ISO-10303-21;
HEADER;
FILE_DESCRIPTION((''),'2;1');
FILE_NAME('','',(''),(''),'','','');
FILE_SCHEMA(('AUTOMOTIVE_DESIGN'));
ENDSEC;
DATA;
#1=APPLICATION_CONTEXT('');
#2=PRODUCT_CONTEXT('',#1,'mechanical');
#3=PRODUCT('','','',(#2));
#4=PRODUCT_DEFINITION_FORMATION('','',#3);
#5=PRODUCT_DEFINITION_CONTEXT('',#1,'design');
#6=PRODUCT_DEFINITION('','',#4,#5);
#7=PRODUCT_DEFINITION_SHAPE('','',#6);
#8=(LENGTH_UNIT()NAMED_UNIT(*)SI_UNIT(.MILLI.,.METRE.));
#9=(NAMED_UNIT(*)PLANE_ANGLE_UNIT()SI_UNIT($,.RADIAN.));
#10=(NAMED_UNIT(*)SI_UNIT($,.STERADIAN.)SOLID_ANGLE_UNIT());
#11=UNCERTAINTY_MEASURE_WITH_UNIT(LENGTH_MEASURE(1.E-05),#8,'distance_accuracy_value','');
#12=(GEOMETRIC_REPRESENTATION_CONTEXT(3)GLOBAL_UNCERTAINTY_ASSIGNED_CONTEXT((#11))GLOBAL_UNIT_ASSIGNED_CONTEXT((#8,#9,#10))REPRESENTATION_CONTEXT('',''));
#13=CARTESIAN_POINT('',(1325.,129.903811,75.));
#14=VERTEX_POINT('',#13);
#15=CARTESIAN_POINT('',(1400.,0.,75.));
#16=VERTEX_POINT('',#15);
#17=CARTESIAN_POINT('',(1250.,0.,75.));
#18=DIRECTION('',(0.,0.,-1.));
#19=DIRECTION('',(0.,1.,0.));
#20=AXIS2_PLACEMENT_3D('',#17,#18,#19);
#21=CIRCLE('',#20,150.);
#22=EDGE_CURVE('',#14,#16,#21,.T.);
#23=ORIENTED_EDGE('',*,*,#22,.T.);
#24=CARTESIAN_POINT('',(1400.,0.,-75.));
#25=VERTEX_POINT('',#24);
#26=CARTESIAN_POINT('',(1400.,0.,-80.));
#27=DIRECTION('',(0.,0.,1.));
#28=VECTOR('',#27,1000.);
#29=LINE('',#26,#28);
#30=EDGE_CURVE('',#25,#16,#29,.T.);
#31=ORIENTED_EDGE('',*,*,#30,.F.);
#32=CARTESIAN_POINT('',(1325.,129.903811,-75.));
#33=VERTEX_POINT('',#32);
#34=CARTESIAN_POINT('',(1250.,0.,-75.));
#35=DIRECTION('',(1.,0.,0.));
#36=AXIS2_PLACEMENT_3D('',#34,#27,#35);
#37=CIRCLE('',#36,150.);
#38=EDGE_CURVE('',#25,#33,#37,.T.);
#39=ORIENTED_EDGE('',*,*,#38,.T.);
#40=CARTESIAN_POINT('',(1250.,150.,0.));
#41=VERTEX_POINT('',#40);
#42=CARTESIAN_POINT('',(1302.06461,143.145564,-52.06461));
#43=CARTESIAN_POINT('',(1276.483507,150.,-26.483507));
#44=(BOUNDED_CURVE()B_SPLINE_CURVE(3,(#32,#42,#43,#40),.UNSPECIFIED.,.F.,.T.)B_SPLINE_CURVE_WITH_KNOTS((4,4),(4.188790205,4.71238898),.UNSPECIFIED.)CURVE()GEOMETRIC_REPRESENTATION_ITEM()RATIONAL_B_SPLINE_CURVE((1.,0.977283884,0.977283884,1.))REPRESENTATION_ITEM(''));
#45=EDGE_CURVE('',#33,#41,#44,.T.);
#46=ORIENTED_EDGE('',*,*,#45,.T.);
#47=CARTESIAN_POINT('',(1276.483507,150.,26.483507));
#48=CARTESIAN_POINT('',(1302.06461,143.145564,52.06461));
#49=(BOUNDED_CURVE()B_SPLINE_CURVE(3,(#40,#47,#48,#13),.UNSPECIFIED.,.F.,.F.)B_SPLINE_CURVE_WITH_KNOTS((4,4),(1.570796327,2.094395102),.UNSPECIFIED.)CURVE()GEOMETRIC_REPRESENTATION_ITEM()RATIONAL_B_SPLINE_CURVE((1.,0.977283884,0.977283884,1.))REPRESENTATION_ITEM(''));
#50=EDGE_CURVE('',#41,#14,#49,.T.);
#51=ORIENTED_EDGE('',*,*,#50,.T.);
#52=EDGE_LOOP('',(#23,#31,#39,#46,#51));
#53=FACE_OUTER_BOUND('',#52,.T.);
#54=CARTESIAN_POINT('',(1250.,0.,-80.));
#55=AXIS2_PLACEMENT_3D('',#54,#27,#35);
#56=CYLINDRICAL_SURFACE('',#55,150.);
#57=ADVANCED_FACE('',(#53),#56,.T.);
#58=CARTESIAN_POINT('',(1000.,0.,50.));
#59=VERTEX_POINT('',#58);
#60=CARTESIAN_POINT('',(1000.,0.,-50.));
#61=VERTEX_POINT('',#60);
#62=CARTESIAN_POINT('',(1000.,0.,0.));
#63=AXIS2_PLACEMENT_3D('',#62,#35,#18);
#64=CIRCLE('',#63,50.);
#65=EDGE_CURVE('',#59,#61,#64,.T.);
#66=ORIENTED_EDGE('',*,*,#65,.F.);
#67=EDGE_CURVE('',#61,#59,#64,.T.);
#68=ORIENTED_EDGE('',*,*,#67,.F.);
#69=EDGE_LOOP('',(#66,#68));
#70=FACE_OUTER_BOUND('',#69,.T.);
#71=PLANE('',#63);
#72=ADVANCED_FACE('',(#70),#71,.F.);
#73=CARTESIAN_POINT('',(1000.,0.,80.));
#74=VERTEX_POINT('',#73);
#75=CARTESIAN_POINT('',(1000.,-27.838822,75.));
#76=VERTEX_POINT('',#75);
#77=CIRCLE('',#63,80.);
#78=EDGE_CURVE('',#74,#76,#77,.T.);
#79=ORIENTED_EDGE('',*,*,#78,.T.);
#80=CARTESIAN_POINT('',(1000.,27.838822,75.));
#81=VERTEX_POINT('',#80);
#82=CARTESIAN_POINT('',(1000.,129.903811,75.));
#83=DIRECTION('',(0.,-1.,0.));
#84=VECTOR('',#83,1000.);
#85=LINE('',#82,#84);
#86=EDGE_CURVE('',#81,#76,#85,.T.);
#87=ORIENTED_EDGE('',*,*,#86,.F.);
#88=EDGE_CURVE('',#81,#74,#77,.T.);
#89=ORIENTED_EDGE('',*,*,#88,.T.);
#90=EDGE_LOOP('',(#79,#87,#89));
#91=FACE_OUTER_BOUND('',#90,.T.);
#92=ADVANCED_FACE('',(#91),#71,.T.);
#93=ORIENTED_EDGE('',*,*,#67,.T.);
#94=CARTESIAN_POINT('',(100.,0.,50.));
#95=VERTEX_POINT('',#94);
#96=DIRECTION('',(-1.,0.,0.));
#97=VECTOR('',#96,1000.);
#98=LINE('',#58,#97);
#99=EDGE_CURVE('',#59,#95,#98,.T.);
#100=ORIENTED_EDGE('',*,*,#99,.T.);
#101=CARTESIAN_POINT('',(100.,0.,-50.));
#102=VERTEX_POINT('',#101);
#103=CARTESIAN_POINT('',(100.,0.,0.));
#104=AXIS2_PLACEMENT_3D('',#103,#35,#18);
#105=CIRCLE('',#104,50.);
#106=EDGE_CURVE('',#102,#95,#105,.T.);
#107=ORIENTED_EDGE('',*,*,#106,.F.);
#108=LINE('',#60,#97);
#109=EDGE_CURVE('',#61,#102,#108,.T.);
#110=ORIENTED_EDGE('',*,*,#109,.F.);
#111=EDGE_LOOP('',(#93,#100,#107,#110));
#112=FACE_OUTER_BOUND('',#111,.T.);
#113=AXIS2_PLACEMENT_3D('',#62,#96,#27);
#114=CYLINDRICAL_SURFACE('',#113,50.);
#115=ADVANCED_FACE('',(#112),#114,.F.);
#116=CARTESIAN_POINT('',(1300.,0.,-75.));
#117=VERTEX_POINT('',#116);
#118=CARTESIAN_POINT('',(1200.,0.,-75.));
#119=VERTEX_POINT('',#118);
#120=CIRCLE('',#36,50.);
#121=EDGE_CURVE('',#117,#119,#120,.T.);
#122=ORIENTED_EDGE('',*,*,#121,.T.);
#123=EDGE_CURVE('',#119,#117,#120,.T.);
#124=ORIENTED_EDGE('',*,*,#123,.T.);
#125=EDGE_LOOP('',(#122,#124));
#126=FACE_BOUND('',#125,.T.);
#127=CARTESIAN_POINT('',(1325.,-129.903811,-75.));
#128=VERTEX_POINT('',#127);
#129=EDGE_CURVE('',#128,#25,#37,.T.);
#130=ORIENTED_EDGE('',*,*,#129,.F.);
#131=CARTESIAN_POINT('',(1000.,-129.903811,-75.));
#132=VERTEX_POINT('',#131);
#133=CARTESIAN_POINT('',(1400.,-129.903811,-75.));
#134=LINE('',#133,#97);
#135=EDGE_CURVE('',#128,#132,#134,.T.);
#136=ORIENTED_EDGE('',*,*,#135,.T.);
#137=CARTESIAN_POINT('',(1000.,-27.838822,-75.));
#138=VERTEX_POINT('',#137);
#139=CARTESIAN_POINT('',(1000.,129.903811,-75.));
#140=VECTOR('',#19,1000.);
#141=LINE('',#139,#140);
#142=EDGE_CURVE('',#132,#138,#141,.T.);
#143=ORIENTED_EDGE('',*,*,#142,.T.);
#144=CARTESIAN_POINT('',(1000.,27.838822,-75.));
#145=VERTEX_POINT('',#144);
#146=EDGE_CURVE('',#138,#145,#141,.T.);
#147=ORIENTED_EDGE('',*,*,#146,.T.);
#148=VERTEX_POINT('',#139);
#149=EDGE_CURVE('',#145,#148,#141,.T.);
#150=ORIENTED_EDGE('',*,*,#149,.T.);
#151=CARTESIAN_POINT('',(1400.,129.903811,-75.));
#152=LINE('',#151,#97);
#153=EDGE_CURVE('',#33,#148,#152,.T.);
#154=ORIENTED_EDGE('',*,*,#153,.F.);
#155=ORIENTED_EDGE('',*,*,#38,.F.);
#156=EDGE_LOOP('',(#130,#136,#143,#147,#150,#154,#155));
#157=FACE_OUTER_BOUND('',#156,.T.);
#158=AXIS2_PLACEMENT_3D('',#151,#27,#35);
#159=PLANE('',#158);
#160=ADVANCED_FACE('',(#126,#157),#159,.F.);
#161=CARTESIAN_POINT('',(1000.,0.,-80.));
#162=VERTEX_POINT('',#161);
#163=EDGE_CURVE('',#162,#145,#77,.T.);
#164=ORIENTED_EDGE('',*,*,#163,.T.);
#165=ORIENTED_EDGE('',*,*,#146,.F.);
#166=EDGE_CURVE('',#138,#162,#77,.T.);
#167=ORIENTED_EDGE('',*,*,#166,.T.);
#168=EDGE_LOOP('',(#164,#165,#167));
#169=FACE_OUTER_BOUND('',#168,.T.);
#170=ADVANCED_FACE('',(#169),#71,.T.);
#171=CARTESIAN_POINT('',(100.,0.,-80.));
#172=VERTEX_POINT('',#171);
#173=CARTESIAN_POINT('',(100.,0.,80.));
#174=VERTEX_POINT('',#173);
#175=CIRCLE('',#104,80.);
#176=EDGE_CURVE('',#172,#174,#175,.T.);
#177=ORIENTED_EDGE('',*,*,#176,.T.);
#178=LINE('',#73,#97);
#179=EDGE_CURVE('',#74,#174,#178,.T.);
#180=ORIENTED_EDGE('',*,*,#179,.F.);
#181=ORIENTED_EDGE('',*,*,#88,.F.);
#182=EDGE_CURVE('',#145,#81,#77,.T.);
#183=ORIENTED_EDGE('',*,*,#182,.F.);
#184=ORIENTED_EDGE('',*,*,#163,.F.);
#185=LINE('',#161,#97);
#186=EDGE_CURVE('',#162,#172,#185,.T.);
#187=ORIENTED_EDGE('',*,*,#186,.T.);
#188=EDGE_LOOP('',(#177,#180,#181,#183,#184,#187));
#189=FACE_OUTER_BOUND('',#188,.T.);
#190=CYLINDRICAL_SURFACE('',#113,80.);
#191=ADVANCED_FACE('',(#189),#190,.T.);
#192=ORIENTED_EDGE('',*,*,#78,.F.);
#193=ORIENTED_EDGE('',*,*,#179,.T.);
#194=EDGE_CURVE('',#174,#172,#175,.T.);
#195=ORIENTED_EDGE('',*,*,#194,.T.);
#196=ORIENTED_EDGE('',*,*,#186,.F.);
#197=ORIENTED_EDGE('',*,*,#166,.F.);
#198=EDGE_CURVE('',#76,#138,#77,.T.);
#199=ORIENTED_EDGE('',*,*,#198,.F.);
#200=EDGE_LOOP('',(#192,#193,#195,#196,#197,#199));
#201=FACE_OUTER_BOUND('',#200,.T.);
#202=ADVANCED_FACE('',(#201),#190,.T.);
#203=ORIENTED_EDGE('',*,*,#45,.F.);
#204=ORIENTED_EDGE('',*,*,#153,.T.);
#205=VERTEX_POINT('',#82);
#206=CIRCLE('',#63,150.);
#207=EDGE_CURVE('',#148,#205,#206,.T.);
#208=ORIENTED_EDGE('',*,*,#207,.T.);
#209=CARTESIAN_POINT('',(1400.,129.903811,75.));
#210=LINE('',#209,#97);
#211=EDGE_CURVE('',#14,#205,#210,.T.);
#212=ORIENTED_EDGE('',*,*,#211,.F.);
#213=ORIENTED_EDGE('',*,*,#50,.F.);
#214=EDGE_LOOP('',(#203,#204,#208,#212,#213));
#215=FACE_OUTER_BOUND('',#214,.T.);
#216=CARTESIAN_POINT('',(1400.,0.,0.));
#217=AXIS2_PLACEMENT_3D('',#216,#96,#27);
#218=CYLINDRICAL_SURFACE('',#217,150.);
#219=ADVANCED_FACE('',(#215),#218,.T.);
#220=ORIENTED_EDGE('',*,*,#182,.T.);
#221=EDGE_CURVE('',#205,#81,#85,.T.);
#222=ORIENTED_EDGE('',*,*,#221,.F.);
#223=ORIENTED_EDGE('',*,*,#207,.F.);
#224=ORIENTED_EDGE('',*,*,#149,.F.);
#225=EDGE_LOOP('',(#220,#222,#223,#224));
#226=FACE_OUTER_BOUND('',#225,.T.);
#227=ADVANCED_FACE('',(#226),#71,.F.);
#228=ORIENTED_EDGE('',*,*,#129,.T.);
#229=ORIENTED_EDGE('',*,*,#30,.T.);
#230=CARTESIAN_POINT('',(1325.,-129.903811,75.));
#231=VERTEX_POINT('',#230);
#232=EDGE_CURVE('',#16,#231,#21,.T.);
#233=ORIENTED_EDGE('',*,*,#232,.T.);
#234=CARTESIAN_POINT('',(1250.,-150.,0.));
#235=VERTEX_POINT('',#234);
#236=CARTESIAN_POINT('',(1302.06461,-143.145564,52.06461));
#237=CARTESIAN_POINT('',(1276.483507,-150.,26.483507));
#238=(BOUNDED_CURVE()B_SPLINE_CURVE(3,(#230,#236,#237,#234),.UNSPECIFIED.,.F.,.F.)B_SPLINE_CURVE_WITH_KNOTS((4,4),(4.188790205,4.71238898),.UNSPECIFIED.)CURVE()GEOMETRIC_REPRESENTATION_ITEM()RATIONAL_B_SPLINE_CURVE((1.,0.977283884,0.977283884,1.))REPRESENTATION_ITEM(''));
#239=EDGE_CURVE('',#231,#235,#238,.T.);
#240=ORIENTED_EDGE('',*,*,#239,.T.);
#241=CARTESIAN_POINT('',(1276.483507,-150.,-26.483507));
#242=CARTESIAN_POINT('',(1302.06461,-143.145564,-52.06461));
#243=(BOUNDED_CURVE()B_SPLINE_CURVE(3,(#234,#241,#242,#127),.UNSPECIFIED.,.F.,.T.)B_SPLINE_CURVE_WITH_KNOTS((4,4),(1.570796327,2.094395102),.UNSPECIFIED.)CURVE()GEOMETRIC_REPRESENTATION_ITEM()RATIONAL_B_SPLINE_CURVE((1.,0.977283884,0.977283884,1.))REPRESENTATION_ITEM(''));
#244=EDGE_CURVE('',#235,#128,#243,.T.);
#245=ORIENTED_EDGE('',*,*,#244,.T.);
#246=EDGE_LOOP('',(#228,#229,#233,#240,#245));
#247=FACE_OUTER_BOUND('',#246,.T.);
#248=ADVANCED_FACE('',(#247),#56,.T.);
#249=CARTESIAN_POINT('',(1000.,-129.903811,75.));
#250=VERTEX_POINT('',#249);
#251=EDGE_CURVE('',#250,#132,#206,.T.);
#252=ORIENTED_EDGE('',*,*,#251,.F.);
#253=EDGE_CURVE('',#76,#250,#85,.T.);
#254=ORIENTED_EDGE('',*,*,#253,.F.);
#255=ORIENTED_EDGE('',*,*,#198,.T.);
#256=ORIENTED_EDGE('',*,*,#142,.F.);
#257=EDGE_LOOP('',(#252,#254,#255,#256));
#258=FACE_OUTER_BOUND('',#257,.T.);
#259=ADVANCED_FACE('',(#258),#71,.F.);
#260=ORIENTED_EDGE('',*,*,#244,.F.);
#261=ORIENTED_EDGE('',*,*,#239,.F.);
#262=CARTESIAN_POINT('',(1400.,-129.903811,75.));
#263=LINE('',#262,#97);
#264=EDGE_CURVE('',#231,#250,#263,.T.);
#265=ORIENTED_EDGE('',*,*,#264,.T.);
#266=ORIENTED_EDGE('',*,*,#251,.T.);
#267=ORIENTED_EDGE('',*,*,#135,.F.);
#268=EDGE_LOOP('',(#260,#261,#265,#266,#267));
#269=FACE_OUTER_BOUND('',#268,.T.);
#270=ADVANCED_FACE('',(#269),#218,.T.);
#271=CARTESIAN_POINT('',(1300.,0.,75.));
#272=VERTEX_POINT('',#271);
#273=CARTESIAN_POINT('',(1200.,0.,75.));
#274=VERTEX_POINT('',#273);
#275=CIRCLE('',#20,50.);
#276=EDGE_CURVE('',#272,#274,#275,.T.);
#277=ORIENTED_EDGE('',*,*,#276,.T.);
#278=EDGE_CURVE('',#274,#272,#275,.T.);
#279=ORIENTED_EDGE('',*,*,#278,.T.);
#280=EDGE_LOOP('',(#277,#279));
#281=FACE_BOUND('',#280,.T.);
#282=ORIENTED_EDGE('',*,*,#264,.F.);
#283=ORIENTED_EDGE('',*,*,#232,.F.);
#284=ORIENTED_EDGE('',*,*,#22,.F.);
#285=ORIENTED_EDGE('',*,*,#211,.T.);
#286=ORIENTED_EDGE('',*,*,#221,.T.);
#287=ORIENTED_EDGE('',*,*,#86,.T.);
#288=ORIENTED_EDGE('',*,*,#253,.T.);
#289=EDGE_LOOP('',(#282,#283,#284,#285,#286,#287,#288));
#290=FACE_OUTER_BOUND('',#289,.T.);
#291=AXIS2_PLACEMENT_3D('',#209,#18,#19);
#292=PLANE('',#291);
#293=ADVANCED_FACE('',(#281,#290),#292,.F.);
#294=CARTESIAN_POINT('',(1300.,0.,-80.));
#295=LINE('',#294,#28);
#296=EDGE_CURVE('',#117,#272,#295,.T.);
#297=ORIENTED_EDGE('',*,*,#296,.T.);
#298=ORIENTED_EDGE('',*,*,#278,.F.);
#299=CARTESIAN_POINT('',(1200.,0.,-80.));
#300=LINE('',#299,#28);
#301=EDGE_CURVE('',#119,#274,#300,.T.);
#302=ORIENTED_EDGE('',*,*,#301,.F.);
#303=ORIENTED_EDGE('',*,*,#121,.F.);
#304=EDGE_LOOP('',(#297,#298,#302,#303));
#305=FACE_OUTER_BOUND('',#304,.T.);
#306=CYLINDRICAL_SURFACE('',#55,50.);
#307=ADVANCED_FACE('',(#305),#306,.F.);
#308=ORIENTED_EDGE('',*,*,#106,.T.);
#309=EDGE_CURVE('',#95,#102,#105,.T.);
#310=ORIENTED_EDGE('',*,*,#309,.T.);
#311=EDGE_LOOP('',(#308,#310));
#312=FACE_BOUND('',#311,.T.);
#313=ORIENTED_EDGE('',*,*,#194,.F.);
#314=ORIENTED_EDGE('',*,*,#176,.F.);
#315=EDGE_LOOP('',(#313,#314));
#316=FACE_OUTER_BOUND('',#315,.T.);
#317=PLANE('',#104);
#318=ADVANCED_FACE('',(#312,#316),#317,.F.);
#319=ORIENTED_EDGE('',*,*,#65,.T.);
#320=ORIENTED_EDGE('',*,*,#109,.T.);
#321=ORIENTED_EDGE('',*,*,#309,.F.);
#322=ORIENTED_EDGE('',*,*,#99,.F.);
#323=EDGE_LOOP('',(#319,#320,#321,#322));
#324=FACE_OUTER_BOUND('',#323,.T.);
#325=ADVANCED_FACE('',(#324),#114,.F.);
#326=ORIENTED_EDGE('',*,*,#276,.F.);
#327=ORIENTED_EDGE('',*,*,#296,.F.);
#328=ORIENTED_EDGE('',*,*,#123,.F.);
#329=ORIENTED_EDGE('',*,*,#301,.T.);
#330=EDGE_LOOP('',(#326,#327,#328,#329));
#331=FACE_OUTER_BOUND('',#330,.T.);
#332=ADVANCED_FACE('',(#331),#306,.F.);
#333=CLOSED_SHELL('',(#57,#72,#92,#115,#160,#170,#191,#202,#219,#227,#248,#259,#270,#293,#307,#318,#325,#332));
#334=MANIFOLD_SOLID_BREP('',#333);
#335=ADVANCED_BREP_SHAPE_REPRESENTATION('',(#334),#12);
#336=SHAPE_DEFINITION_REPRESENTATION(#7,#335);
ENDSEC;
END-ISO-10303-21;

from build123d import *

# Parameters (mm, degrees)
BOSS_EXTRUDE1_START     = 100
SKETCH1_R               = 80
SKETCH1_R_2             = 50
BOSS_EXTRUDE1_DEPTH     = 900
BOSS_EXTRUDE2_DEPTH     = 400
CUT_EXTRUDE2_DEPTH      = 1417.518619715
CUT_EXTRUDE2_DEPTH_BACK = 1417.518619715
CUT_EXTRUDE3_DEPTH      = 1417.518619715
CUT_EXTRUDE3_DEPTH_BACK = 1417.518619715
SKETCH_4_5_2_R          = 50


with BuildPart() as part:
    # Sketch1 → Boss-Extrude1 (new body)
    with BuildSketch(Plane(origin=(0, 0, 0), x_dir=(0, 0, -1), z_dir=(1, 0, 0)).offset(BOSS_EXTRUDE1_START)):
        Circle(SKETCH1_R)
        Circle(SKETCH1_R_2, mode=Mode.SUBTRACT)
    extrude(amount=BOSS_EXTRUDE1_DEPTH)

    # Sketch3 → Boss-Extrude2 (add)
    with BuildSketch(Plane(origin=(1000, 0, 0), x_dir=(0, 0, -1), z_dir=(1, 0, 0))):
        with BuildLine():
            Line((-75, 129.903810568), (-75, -129.903810568))
            ThreePointArc((-75, -129.903810568), (0, -150), (75, -129.903810568))
            Line((75, -129.903810568), (75, 129.903810568))
            ThreePointArc((75, 129.903810568), (0, 150), (-75, 129.903810568))
        make_face()
    extrude(amount=BOSS_EXTRUDE2_DEPTH)

    # Sketch 4_5 → Cut-Extrude2 (cut, two sides: drawn at the far end of the back side and taken through both)
    with BuildSketch(Plane.XY.offset(75).offset(-CUT_EXTRUDE2_DEPTH_BACK)):
        with BuildLine():
            Line((1250, 150), (1455.357524725, 150))
            Line((1455.357524725, 150), (1455.357524725, -150))
            Line((1455.357524725, -150), (1250, -150))
            ThreePointArc((1250, -150), (1400, 0), (1250, 150))
        make_face()
    extrude(amount=CUT_EXTRUDE2_DEPTH + CUT_EXTRUDE2_DEPTH_BACK, mode=Mode.SUBTRACT)

    # Sketch 4_5 2 → Cut-Extrude3 (cut, two sides: drawn at the far end of the back side and taken through both)
    with BuildSketch(Plane.XY.offset(75).offset(-CUT_EXTRUDE3_DEPTH_BACK)):
        with Locations((1250, 0)):
            Circle(SKETCH_4_5_2_R)
    extrude(amount=CUT_EXTRUDE3_DEPTH + CUT_EXTRUDE3_DEPTH_BACK, mode=Mode.SUBTRACT)


solid = part.part
